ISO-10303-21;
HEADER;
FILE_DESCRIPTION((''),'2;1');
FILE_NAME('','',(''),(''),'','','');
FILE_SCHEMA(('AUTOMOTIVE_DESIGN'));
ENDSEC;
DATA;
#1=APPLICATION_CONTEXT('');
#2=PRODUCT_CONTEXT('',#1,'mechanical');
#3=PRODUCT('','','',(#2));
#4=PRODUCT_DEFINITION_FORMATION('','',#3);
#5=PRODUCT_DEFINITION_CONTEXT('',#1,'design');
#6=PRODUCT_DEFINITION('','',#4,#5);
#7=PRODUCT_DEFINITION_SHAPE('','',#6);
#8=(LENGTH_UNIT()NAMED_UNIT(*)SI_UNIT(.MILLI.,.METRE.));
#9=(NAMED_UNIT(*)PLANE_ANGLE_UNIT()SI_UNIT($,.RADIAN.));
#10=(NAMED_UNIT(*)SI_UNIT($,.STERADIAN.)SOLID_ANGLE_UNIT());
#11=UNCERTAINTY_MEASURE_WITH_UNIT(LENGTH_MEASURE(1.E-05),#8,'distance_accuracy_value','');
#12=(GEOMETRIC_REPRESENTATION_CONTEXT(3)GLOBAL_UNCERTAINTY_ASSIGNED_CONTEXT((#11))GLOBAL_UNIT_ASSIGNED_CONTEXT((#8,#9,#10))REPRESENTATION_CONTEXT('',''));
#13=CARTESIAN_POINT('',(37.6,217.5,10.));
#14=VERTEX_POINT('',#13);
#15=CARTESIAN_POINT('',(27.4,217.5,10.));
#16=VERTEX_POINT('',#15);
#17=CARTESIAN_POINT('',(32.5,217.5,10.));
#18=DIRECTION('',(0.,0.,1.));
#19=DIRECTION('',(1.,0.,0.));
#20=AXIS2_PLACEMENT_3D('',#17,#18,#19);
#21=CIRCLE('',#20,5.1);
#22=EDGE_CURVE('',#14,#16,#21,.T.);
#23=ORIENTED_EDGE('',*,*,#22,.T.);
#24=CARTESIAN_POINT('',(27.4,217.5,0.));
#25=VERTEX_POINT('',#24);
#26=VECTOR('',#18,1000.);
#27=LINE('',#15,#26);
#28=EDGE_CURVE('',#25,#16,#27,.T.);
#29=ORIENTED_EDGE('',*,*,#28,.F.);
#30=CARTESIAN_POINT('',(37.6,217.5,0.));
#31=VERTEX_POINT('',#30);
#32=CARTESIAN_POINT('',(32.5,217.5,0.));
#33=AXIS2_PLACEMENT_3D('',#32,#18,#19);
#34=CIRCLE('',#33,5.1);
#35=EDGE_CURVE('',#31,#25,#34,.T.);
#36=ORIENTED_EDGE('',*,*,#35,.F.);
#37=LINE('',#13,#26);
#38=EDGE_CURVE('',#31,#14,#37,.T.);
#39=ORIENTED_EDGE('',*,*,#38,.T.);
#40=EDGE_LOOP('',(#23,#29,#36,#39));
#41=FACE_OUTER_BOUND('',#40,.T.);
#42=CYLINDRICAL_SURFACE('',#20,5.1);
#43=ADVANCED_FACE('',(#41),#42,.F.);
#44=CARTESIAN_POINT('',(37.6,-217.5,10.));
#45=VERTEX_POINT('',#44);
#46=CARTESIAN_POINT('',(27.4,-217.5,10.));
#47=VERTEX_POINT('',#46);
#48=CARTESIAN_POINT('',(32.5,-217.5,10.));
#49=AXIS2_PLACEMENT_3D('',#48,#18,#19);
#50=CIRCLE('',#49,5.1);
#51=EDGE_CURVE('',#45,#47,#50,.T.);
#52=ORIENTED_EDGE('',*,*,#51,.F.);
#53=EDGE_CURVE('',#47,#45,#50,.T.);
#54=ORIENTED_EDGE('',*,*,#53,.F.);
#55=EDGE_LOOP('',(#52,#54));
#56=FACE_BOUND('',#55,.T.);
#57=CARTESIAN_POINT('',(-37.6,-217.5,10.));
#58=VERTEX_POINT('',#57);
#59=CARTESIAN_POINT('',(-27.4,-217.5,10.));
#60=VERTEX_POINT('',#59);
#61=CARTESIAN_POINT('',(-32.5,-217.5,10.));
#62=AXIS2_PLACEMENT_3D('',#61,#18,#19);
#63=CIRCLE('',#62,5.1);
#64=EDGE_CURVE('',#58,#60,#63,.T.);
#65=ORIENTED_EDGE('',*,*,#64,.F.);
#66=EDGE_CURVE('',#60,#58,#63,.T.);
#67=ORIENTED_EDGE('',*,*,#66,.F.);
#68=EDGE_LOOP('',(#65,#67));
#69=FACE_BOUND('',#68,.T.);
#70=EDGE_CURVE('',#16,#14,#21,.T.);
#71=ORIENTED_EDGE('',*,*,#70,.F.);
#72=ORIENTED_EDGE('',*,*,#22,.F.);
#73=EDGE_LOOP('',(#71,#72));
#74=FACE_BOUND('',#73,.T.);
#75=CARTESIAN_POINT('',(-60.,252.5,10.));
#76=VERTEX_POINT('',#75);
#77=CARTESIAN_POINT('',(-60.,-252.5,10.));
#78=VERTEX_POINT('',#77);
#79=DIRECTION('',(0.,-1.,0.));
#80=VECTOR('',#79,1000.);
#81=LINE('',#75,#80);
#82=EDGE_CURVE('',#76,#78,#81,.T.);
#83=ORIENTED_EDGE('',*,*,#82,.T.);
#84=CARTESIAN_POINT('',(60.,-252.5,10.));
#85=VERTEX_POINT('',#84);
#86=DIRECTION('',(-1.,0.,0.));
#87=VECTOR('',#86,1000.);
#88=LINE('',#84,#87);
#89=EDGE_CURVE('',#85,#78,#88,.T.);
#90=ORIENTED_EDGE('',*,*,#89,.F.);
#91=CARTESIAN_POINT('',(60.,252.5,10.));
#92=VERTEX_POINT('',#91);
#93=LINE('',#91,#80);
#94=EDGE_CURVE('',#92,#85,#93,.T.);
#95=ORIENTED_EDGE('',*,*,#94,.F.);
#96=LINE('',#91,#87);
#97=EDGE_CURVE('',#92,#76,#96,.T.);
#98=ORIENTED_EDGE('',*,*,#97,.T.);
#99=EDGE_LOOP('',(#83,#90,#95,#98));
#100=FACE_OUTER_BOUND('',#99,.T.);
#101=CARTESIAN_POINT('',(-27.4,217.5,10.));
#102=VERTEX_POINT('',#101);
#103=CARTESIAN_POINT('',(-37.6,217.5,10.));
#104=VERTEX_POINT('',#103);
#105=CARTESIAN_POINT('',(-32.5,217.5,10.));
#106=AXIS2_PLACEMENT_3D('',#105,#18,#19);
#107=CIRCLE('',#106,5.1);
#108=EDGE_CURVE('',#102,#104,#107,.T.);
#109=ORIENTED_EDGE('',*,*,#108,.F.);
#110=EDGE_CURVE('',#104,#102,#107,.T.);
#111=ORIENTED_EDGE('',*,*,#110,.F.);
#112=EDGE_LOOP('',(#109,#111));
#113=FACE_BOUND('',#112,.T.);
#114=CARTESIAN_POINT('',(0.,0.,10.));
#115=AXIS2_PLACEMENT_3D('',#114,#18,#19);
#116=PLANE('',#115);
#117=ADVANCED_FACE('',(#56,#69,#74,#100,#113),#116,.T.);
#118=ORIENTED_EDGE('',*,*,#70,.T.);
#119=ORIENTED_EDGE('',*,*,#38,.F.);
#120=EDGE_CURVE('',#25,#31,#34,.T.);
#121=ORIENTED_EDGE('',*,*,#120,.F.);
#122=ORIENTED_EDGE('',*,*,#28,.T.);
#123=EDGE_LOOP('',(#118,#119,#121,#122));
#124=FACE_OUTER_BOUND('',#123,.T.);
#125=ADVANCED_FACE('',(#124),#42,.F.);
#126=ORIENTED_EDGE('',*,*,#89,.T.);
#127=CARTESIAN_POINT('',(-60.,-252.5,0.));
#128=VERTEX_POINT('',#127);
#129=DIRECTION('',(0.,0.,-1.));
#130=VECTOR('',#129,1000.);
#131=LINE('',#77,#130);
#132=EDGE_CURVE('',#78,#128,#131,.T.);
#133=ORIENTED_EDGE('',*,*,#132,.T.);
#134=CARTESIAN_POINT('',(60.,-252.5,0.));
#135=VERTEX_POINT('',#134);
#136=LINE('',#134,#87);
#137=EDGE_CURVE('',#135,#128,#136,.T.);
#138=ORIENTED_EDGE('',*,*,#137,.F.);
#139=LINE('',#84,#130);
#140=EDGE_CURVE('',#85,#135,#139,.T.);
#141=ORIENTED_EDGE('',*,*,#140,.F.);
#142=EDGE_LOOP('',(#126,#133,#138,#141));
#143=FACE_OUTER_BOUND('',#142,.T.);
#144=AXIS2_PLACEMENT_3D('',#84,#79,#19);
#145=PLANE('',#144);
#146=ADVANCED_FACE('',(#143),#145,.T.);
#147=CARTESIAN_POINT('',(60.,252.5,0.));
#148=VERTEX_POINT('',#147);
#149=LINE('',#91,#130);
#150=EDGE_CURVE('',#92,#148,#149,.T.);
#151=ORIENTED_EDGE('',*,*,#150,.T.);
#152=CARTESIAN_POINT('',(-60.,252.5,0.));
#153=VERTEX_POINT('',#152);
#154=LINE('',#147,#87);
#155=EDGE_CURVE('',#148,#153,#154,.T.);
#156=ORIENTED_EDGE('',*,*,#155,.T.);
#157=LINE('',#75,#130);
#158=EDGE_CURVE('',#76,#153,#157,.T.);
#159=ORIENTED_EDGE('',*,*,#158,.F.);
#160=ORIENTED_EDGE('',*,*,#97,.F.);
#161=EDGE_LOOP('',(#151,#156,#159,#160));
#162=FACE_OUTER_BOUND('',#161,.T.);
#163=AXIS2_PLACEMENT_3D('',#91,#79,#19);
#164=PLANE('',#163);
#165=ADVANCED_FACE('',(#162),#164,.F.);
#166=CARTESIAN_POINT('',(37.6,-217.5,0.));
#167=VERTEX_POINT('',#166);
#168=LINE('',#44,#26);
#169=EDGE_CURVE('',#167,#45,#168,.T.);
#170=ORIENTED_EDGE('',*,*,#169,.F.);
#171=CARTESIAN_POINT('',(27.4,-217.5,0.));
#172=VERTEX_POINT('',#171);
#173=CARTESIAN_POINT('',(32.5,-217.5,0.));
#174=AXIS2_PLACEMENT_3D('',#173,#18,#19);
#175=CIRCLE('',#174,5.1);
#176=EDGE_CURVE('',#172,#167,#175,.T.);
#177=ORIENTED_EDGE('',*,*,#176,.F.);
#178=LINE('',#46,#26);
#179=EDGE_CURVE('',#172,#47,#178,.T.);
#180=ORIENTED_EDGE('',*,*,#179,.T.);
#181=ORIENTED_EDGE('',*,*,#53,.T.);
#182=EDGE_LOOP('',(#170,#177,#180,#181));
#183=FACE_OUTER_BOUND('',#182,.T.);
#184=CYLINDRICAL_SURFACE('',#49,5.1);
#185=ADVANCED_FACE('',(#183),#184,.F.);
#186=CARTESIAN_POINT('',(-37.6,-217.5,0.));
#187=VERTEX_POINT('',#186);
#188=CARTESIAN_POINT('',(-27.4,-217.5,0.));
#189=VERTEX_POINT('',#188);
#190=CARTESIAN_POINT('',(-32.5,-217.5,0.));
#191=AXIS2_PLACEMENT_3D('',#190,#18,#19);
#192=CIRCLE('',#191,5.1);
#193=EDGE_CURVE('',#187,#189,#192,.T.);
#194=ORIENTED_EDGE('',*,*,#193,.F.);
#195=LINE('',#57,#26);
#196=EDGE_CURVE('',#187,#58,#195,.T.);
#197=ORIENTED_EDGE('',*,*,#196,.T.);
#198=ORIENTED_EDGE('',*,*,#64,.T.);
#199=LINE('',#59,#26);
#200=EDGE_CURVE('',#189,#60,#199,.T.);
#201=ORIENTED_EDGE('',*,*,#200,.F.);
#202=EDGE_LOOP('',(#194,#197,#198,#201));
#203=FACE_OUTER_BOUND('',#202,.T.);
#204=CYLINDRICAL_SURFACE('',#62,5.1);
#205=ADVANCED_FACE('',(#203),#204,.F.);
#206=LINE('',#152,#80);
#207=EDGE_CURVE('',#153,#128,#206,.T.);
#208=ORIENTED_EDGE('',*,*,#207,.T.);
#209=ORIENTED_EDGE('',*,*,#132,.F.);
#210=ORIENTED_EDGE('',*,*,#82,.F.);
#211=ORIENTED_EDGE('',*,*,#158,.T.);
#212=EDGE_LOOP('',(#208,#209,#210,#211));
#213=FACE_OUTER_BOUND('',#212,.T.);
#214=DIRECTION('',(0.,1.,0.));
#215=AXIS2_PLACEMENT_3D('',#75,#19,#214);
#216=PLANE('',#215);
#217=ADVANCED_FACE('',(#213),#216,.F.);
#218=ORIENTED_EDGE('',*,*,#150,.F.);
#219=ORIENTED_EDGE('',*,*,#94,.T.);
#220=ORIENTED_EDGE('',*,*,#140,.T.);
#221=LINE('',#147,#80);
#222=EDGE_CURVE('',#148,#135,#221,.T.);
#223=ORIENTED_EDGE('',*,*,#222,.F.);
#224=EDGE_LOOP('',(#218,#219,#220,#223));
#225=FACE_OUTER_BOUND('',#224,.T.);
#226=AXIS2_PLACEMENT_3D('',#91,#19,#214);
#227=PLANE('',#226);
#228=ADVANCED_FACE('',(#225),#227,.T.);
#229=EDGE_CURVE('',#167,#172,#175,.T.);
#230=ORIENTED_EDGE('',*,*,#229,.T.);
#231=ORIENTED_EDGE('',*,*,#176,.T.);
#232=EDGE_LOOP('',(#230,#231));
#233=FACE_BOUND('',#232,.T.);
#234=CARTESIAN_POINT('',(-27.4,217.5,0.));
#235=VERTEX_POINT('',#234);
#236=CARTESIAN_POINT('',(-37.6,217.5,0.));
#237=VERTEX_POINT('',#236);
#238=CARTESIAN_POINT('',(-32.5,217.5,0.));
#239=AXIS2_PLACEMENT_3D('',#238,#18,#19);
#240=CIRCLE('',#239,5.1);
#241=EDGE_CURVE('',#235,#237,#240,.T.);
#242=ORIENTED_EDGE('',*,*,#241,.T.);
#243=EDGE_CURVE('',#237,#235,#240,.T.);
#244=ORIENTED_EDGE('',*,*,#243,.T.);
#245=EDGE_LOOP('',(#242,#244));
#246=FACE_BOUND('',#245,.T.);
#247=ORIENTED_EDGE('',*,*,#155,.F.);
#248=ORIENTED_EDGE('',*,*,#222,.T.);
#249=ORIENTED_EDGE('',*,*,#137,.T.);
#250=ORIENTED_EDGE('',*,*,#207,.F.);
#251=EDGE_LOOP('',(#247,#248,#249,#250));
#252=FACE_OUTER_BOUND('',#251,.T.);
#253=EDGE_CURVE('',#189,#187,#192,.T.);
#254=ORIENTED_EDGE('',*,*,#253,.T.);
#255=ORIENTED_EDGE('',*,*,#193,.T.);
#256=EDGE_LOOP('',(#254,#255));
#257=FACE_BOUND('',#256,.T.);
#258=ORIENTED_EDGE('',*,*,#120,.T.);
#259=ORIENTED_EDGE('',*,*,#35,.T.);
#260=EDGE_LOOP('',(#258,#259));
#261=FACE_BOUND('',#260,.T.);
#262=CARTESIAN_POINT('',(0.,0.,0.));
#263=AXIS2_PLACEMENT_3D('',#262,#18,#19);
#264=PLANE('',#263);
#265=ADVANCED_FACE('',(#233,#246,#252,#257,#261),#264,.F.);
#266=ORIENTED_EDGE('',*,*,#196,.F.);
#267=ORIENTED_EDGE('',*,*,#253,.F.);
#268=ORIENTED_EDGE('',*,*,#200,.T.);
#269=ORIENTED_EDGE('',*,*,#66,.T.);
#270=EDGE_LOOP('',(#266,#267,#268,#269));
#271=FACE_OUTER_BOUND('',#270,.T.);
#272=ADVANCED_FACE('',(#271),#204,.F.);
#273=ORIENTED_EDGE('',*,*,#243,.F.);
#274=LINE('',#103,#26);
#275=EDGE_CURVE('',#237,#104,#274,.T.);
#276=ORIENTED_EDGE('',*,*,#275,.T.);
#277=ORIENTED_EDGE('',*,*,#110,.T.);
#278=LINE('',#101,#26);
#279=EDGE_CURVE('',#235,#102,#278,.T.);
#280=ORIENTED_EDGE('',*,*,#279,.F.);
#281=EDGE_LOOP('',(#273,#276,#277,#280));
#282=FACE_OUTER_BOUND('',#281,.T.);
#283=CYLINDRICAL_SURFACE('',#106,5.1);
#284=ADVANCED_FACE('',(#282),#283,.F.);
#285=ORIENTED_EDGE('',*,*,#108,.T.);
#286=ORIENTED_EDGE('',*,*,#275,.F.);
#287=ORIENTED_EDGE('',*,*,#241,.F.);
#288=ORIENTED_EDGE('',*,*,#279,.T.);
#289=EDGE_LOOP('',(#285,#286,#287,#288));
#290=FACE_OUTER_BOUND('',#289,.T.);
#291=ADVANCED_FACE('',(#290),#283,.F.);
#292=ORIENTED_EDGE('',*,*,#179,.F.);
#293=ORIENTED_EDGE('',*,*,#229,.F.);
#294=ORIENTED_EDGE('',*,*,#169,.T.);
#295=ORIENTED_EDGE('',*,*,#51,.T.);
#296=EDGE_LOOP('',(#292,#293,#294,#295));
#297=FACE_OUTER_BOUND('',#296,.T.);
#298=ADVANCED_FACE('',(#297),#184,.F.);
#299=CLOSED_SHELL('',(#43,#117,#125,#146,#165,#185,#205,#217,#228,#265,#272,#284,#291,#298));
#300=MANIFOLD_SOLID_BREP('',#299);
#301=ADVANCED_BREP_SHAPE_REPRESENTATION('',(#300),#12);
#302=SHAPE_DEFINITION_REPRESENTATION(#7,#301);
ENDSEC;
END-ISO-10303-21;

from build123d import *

# Parameters (mm, degrees)
SKETCH1_W              = 120
SKETCH1_H              = 505
BOSS_EXTRUDE1_DEPTH    = 10
M12_TAPPED_HOLE1_D     = 10.2
M12_TAPPED_HOLE1_DEPTH = 29.25
M12_TAPPED_HOLE1_TIP   = 3.064389157


with BuildPart() as part:
    # Sketch1 → Boss-Extrude1 (new body)
    with BuildSketch(Plane.XY):
        Rectangle(SKETCH1_W, SKETCH1_H)
    extrude(amount=BOSS_EXTRUDE1_DEPTH)

    # M12 Tapped Hole1
    with Locations(Plane.XY.offset(10)):
        with Locations((-32.5, 217.5), (32.5, 217.5), (32.5, -217.5), (-32.5, -217.5)):
            Hole(M12_TAPPED_HOLE1_D / 2, depth=M12_TAPPED_HOLE1_DEPTH)
            with Locations((0, 0, -(M12_TAPPED_HOLE1_DEPTH + M12_TAPPED_HOLE1_TIP / 2))):  # 118° drill point
                Cone(0, M12_TAPPED_HOLE1_D / 2, M12_TAPPED_HOLE1_TIP, mode=Mode.SUBTRACT)


solid = part.part
